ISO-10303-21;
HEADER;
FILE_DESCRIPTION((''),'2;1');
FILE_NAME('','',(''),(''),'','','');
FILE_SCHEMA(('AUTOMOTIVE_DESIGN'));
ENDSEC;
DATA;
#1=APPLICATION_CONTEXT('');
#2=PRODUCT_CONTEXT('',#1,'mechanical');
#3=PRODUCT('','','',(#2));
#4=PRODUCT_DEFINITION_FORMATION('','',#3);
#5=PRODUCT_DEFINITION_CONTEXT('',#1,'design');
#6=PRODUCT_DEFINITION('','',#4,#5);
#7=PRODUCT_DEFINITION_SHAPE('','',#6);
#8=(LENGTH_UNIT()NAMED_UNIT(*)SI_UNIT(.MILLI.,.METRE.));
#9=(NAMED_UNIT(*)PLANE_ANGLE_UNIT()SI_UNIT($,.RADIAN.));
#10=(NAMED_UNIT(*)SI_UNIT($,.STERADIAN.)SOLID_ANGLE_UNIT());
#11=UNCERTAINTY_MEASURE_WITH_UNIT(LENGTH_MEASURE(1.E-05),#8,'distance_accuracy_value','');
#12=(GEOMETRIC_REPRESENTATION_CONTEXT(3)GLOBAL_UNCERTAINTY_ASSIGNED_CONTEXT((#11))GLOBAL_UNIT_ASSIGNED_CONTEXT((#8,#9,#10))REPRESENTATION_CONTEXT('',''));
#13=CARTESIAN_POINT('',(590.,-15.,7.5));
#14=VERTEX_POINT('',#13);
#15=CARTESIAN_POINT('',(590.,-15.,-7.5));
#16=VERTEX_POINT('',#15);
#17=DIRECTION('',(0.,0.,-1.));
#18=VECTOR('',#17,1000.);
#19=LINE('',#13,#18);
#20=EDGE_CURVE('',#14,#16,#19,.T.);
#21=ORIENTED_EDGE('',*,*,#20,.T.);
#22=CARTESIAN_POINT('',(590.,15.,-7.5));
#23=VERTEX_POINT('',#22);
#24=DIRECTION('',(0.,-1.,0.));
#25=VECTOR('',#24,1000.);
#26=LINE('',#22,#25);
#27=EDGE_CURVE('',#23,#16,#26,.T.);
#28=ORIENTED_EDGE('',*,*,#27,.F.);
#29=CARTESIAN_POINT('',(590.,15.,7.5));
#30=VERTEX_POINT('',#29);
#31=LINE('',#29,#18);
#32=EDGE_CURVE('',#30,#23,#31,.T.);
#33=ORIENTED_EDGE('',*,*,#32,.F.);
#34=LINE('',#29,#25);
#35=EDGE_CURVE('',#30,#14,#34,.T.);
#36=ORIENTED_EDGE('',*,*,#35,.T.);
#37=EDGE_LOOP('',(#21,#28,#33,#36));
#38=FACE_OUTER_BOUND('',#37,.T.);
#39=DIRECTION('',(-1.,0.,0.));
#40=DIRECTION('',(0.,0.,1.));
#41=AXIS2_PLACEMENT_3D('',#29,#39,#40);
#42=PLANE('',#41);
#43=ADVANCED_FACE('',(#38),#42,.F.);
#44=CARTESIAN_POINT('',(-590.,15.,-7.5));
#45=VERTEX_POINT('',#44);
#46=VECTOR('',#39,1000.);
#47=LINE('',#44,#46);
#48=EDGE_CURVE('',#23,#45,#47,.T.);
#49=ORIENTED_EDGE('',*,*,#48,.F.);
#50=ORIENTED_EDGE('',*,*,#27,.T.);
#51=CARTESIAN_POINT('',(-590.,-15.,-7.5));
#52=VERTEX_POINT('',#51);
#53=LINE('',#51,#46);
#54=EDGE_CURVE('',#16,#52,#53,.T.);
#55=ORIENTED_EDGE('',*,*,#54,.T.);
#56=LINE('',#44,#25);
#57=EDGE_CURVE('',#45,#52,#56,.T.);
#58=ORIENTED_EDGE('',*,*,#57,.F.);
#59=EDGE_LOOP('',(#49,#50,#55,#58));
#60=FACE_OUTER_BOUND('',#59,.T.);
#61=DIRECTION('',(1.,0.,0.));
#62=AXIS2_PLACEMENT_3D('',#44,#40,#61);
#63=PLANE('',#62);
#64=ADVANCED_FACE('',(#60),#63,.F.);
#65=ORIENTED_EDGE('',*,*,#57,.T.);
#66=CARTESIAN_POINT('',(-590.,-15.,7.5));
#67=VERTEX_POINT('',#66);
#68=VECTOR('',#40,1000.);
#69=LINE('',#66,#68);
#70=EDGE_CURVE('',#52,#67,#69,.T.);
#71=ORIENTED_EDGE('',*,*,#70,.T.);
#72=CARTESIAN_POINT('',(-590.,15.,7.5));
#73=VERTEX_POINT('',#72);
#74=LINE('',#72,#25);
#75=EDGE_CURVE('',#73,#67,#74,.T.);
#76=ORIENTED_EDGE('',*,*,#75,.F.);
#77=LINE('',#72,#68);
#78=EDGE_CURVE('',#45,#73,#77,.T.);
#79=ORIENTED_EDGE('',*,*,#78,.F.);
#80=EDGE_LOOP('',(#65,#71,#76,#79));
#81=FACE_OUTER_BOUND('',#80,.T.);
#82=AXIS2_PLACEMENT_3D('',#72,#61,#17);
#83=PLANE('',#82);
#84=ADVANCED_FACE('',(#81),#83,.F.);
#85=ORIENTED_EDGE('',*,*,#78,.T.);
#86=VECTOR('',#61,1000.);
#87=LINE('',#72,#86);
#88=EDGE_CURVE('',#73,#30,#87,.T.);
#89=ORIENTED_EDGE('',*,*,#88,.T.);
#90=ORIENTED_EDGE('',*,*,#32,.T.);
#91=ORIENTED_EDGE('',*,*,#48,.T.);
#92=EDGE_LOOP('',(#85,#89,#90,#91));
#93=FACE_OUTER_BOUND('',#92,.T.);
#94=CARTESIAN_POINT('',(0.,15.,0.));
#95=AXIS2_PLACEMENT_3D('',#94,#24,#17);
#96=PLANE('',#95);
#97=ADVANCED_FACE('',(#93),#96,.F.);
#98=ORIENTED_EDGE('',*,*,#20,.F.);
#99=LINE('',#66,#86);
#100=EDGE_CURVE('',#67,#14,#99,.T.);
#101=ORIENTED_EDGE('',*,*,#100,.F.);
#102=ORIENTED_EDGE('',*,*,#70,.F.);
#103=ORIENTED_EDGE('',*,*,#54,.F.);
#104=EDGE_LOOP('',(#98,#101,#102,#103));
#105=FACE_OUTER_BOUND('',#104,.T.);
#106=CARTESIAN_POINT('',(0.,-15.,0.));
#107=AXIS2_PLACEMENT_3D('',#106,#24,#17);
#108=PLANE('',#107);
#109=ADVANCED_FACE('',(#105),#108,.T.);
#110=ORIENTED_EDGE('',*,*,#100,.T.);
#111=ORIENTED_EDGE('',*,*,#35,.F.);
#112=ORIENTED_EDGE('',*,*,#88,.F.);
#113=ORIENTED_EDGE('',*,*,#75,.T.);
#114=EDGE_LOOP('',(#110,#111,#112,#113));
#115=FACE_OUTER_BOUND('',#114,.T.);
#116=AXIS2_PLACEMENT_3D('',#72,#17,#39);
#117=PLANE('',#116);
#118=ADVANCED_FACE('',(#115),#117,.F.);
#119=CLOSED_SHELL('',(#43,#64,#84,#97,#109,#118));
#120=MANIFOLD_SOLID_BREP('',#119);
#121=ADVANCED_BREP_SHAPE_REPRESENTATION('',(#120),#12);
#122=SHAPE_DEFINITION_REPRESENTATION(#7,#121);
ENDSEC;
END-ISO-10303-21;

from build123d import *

# Parameters (mm, degrees)
SKETCH_1_W      = 1180
SKETCH_1_H      = 15
EXTRUDE_1_DEPTH = 15


with BuildPart() as part:
    # 草图1 → 凸台-拉伸1 (new, symmetric)
    with BuildSketch(Plane(origin=(0, 0, 0), x_dir=(1, 0, 0), z_dir=(0, 1, 0))):
        Rectangle(SKETCH_1_W, SKETCH_1_H)
    extrude(amount=EXTRUDE_1_DEPTH, both=True)


solid = part.part
